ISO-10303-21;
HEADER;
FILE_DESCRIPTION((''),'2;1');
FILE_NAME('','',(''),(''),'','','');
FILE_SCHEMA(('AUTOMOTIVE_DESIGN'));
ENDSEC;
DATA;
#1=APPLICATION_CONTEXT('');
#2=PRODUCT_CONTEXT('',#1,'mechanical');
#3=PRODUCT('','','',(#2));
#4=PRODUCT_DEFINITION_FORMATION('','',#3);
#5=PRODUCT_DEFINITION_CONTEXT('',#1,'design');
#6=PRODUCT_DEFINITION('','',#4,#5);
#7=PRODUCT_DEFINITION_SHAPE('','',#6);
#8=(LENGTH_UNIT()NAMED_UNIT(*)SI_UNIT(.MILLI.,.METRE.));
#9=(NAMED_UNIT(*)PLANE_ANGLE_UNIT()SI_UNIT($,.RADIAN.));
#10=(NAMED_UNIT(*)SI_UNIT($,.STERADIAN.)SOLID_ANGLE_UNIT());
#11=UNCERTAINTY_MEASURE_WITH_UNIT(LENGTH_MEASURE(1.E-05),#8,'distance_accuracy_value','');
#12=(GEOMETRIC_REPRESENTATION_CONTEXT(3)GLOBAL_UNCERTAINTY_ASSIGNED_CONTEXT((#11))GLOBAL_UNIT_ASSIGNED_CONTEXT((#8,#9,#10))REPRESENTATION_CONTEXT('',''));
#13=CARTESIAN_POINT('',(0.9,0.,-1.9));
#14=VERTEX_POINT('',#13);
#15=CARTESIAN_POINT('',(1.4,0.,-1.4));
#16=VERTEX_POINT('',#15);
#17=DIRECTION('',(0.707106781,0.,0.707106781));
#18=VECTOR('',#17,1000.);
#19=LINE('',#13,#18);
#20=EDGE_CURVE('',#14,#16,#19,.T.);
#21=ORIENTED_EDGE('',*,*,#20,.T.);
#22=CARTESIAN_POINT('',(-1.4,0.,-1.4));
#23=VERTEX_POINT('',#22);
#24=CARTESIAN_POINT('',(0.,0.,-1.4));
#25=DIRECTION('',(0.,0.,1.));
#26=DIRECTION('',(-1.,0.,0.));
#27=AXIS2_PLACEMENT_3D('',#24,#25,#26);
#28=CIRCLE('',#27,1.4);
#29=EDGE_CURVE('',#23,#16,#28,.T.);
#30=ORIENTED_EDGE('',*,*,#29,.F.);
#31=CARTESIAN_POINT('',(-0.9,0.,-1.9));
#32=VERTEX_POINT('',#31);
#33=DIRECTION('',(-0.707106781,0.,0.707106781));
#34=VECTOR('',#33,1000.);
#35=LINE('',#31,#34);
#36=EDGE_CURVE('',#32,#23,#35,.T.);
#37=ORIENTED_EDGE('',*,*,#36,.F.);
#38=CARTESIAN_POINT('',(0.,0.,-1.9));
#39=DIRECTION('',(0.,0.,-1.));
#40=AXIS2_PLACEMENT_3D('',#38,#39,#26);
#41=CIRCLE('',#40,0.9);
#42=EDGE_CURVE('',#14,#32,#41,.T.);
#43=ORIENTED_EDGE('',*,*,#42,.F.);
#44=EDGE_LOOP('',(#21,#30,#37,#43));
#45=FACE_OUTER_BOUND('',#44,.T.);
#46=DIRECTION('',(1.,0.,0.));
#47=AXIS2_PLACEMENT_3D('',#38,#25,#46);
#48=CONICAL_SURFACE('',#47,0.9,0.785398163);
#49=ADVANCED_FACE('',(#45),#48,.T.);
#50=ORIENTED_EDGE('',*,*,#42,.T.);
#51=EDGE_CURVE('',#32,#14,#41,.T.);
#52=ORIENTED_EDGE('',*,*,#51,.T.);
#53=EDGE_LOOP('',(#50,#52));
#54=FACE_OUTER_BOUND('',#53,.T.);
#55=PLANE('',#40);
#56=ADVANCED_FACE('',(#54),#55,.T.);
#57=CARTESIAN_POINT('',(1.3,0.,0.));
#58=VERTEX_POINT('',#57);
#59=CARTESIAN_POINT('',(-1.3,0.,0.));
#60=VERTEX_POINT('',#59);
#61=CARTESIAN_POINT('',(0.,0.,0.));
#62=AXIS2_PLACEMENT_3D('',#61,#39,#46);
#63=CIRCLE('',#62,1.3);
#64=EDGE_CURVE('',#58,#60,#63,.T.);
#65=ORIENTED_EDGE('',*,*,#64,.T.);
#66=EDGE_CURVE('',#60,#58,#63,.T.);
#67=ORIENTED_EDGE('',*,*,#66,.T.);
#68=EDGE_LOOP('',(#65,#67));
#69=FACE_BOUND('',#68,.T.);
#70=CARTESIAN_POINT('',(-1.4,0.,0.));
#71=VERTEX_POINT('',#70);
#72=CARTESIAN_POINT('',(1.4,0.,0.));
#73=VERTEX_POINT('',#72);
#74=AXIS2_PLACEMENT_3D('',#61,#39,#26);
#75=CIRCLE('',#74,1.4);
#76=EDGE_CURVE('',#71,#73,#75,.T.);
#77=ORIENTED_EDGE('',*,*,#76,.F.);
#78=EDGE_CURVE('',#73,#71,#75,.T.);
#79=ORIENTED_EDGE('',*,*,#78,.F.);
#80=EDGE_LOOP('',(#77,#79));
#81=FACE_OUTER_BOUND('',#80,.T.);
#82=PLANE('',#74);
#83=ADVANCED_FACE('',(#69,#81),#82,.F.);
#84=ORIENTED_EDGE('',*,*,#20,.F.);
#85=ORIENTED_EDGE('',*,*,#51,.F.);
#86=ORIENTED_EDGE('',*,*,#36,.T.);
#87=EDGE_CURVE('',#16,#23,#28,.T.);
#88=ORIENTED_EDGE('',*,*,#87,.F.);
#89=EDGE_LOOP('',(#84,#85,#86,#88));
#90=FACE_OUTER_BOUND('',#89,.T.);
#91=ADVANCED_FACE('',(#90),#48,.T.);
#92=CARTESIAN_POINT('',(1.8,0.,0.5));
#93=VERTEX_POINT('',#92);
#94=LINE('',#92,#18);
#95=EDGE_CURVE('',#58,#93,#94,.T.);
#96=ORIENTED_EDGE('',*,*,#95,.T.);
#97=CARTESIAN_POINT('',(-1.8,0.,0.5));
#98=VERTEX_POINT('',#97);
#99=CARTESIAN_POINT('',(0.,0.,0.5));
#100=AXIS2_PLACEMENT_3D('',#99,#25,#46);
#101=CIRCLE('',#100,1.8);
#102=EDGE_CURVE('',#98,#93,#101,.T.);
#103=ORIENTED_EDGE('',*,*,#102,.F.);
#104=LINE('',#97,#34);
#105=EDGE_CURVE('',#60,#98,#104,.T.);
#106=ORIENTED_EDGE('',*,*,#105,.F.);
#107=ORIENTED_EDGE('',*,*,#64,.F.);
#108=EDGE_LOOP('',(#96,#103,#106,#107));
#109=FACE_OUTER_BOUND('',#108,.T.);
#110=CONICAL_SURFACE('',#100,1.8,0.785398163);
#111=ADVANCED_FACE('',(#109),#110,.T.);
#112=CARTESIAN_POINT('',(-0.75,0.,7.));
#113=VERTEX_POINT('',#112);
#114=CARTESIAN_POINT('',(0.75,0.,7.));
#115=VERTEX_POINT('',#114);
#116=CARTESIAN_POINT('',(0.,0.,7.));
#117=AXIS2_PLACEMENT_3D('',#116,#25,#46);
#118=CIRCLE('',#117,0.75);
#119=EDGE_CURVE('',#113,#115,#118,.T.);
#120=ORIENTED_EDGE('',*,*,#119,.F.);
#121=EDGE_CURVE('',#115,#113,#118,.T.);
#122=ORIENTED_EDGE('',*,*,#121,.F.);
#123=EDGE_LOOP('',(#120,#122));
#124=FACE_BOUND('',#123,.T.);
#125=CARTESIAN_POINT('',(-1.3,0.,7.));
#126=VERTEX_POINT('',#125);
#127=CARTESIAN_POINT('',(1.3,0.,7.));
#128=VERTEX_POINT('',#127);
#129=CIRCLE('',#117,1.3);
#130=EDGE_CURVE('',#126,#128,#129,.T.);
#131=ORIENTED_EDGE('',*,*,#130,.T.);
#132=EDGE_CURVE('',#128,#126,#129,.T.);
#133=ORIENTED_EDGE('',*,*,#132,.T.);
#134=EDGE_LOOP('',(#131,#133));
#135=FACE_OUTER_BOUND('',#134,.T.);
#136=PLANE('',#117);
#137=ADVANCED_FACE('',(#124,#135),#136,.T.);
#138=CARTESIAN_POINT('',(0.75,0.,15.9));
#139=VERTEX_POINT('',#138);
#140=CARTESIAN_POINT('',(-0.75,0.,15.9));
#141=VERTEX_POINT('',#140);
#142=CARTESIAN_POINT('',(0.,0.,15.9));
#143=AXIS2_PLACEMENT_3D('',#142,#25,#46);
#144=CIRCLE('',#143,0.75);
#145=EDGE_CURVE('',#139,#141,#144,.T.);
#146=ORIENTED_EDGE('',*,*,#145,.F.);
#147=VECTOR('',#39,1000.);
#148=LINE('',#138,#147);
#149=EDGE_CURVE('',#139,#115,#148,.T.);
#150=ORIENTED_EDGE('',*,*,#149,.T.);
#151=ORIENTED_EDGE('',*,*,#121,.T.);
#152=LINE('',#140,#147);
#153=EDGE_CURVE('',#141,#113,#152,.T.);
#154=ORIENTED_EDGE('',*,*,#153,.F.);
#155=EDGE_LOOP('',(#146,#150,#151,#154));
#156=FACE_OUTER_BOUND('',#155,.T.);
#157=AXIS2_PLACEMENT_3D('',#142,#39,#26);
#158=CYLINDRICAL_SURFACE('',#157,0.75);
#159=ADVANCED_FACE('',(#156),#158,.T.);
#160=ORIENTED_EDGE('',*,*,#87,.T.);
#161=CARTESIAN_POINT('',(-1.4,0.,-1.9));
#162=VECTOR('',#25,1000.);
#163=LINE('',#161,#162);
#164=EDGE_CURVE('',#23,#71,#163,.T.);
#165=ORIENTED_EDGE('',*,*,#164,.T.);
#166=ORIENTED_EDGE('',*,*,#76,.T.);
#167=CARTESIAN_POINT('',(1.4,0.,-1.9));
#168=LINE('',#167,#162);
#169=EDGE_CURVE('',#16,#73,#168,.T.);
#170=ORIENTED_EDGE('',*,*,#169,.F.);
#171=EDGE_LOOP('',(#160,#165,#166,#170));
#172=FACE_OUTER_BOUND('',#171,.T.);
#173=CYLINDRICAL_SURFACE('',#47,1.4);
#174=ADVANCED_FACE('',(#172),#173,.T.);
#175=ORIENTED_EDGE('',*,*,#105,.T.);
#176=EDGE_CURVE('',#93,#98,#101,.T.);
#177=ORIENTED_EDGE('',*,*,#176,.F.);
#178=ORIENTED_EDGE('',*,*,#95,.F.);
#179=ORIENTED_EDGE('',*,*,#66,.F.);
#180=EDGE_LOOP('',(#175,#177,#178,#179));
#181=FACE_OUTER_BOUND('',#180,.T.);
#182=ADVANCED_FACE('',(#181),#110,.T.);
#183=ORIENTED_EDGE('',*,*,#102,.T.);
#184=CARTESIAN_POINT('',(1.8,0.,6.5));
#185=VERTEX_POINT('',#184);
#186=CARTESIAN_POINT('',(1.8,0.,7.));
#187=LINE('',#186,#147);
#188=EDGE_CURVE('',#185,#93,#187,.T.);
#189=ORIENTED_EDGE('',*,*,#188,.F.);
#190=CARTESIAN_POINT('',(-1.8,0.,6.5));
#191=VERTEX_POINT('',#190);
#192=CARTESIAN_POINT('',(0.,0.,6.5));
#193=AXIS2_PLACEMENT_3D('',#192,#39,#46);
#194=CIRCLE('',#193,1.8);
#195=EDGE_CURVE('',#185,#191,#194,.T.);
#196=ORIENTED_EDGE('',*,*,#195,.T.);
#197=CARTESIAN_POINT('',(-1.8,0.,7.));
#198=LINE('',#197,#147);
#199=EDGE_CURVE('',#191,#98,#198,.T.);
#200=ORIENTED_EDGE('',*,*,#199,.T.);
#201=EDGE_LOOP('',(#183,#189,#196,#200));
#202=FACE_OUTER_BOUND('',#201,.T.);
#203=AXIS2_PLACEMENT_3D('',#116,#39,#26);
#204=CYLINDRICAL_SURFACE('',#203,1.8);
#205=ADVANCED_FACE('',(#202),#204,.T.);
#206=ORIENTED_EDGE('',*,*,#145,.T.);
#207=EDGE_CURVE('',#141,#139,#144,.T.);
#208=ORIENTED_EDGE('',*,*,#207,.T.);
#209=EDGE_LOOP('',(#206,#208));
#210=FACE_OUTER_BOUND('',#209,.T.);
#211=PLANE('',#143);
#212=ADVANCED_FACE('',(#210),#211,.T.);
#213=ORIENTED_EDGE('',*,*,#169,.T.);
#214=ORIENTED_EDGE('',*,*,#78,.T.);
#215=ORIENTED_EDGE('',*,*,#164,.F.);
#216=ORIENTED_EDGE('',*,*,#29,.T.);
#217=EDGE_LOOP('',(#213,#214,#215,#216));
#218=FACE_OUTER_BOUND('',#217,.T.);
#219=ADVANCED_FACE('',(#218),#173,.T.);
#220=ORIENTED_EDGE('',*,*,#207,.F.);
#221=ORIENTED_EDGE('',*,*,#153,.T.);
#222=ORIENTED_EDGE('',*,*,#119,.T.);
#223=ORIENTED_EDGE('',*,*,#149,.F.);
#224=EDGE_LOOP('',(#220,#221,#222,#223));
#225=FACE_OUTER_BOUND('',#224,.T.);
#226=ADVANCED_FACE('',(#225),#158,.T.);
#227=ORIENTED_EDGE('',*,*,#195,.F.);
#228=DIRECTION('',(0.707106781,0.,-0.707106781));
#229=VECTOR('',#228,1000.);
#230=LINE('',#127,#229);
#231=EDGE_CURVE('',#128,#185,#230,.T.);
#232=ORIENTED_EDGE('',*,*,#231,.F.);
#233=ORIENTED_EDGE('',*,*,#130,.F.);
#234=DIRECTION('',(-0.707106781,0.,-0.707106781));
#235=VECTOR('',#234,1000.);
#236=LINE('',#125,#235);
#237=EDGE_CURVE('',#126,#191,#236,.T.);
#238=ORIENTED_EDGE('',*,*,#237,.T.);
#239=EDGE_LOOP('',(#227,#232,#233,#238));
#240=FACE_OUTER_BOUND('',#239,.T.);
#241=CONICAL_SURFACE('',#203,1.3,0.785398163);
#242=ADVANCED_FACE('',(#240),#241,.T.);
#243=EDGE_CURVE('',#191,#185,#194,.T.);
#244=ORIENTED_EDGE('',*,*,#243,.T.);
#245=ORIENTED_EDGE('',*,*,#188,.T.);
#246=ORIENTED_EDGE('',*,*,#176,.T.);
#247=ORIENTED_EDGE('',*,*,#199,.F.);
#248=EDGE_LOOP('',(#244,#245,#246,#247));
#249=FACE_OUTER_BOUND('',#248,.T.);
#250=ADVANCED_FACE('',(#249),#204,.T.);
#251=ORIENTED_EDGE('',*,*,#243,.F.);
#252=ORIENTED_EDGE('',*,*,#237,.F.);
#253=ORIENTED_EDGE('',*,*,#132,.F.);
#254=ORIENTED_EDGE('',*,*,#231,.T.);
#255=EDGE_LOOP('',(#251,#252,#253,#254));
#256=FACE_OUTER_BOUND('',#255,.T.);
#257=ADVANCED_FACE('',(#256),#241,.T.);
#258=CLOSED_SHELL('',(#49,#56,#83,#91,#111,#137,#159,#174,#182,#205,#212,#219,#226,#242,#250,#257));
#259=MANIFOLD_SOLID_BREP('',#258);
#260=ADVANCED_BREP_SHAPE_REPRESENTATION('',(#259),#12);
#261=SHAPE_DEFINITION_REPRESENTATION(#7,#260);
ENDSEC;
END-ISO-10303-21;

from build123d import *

# Parameters (mm, degrees)
SKETCH_2_R      = 1.8
EXTRUDE_1_DEPTH = 7
SKETCH_3_R      = 0.75
EXTRUDE_2_DEPTH = 8.9
CHAMFER_1_SIZE  = 0.5
CHAMFER_2_SIZE  = 0.5
SKETCH_4_R      = 1.4
EXTRUDE_3_DEPTH = 1.9
CHAMFER_3_SIZE  = 0.5


with BuildPart() as part:
    # 草图2 → 拉伸1 (new body)
    with BuildSketch(Plane.XY):
        Circle(SKETCH_2_R)
    extrude(amount=EXTRUDE_1_DEPTH)

    # 草图3 → 拉伸2 (add)
    with BuildSketch(Plane.XY.offset(7)):
        Circle(SKETCH_3_R)
    extrude(amount=EXTRUDE_2_DEPTH)

    # 倒角1
    chamfer_1_edges = [part.edges().sort_by_distance(p)[0] for p in [
        (-1.8, 0, 0),
    ]]
    chamfer(chamfer_1_edges, length=CHAMFER_1_SIZE)

    # 倒角2
    chamfer_2_edges = [part.edges().sort_by_distance(p)[0] for p in [
        (-1.8, 0, 7),
    ]]
    chamfer(chamfer_2_edges, length=CHAMFER_2_SIZE)

    # 草图4 → 拉伸3 (add)
    with BuildSketch(Plane(origin=(0, 0, 0), x_dir=(-1, 0, 0), z_dir=(0, 0, -1))):
        with Locations(Location((0, 0, 0), (0, 0, 180))):
            Circle(SKETCH_4_R)
    extrude(amount=EXTRUDE_3_DEPTH)

    # 倒角3
    chamfer_3_edges = [part.edges().sort_by_distance(p)[0] for p in [
        (-1.4, 0, -1.9),
    ]]
    chamfer(chamfer_3_edges, length=CHAMFER_3_SIZE)


solid = part.part
